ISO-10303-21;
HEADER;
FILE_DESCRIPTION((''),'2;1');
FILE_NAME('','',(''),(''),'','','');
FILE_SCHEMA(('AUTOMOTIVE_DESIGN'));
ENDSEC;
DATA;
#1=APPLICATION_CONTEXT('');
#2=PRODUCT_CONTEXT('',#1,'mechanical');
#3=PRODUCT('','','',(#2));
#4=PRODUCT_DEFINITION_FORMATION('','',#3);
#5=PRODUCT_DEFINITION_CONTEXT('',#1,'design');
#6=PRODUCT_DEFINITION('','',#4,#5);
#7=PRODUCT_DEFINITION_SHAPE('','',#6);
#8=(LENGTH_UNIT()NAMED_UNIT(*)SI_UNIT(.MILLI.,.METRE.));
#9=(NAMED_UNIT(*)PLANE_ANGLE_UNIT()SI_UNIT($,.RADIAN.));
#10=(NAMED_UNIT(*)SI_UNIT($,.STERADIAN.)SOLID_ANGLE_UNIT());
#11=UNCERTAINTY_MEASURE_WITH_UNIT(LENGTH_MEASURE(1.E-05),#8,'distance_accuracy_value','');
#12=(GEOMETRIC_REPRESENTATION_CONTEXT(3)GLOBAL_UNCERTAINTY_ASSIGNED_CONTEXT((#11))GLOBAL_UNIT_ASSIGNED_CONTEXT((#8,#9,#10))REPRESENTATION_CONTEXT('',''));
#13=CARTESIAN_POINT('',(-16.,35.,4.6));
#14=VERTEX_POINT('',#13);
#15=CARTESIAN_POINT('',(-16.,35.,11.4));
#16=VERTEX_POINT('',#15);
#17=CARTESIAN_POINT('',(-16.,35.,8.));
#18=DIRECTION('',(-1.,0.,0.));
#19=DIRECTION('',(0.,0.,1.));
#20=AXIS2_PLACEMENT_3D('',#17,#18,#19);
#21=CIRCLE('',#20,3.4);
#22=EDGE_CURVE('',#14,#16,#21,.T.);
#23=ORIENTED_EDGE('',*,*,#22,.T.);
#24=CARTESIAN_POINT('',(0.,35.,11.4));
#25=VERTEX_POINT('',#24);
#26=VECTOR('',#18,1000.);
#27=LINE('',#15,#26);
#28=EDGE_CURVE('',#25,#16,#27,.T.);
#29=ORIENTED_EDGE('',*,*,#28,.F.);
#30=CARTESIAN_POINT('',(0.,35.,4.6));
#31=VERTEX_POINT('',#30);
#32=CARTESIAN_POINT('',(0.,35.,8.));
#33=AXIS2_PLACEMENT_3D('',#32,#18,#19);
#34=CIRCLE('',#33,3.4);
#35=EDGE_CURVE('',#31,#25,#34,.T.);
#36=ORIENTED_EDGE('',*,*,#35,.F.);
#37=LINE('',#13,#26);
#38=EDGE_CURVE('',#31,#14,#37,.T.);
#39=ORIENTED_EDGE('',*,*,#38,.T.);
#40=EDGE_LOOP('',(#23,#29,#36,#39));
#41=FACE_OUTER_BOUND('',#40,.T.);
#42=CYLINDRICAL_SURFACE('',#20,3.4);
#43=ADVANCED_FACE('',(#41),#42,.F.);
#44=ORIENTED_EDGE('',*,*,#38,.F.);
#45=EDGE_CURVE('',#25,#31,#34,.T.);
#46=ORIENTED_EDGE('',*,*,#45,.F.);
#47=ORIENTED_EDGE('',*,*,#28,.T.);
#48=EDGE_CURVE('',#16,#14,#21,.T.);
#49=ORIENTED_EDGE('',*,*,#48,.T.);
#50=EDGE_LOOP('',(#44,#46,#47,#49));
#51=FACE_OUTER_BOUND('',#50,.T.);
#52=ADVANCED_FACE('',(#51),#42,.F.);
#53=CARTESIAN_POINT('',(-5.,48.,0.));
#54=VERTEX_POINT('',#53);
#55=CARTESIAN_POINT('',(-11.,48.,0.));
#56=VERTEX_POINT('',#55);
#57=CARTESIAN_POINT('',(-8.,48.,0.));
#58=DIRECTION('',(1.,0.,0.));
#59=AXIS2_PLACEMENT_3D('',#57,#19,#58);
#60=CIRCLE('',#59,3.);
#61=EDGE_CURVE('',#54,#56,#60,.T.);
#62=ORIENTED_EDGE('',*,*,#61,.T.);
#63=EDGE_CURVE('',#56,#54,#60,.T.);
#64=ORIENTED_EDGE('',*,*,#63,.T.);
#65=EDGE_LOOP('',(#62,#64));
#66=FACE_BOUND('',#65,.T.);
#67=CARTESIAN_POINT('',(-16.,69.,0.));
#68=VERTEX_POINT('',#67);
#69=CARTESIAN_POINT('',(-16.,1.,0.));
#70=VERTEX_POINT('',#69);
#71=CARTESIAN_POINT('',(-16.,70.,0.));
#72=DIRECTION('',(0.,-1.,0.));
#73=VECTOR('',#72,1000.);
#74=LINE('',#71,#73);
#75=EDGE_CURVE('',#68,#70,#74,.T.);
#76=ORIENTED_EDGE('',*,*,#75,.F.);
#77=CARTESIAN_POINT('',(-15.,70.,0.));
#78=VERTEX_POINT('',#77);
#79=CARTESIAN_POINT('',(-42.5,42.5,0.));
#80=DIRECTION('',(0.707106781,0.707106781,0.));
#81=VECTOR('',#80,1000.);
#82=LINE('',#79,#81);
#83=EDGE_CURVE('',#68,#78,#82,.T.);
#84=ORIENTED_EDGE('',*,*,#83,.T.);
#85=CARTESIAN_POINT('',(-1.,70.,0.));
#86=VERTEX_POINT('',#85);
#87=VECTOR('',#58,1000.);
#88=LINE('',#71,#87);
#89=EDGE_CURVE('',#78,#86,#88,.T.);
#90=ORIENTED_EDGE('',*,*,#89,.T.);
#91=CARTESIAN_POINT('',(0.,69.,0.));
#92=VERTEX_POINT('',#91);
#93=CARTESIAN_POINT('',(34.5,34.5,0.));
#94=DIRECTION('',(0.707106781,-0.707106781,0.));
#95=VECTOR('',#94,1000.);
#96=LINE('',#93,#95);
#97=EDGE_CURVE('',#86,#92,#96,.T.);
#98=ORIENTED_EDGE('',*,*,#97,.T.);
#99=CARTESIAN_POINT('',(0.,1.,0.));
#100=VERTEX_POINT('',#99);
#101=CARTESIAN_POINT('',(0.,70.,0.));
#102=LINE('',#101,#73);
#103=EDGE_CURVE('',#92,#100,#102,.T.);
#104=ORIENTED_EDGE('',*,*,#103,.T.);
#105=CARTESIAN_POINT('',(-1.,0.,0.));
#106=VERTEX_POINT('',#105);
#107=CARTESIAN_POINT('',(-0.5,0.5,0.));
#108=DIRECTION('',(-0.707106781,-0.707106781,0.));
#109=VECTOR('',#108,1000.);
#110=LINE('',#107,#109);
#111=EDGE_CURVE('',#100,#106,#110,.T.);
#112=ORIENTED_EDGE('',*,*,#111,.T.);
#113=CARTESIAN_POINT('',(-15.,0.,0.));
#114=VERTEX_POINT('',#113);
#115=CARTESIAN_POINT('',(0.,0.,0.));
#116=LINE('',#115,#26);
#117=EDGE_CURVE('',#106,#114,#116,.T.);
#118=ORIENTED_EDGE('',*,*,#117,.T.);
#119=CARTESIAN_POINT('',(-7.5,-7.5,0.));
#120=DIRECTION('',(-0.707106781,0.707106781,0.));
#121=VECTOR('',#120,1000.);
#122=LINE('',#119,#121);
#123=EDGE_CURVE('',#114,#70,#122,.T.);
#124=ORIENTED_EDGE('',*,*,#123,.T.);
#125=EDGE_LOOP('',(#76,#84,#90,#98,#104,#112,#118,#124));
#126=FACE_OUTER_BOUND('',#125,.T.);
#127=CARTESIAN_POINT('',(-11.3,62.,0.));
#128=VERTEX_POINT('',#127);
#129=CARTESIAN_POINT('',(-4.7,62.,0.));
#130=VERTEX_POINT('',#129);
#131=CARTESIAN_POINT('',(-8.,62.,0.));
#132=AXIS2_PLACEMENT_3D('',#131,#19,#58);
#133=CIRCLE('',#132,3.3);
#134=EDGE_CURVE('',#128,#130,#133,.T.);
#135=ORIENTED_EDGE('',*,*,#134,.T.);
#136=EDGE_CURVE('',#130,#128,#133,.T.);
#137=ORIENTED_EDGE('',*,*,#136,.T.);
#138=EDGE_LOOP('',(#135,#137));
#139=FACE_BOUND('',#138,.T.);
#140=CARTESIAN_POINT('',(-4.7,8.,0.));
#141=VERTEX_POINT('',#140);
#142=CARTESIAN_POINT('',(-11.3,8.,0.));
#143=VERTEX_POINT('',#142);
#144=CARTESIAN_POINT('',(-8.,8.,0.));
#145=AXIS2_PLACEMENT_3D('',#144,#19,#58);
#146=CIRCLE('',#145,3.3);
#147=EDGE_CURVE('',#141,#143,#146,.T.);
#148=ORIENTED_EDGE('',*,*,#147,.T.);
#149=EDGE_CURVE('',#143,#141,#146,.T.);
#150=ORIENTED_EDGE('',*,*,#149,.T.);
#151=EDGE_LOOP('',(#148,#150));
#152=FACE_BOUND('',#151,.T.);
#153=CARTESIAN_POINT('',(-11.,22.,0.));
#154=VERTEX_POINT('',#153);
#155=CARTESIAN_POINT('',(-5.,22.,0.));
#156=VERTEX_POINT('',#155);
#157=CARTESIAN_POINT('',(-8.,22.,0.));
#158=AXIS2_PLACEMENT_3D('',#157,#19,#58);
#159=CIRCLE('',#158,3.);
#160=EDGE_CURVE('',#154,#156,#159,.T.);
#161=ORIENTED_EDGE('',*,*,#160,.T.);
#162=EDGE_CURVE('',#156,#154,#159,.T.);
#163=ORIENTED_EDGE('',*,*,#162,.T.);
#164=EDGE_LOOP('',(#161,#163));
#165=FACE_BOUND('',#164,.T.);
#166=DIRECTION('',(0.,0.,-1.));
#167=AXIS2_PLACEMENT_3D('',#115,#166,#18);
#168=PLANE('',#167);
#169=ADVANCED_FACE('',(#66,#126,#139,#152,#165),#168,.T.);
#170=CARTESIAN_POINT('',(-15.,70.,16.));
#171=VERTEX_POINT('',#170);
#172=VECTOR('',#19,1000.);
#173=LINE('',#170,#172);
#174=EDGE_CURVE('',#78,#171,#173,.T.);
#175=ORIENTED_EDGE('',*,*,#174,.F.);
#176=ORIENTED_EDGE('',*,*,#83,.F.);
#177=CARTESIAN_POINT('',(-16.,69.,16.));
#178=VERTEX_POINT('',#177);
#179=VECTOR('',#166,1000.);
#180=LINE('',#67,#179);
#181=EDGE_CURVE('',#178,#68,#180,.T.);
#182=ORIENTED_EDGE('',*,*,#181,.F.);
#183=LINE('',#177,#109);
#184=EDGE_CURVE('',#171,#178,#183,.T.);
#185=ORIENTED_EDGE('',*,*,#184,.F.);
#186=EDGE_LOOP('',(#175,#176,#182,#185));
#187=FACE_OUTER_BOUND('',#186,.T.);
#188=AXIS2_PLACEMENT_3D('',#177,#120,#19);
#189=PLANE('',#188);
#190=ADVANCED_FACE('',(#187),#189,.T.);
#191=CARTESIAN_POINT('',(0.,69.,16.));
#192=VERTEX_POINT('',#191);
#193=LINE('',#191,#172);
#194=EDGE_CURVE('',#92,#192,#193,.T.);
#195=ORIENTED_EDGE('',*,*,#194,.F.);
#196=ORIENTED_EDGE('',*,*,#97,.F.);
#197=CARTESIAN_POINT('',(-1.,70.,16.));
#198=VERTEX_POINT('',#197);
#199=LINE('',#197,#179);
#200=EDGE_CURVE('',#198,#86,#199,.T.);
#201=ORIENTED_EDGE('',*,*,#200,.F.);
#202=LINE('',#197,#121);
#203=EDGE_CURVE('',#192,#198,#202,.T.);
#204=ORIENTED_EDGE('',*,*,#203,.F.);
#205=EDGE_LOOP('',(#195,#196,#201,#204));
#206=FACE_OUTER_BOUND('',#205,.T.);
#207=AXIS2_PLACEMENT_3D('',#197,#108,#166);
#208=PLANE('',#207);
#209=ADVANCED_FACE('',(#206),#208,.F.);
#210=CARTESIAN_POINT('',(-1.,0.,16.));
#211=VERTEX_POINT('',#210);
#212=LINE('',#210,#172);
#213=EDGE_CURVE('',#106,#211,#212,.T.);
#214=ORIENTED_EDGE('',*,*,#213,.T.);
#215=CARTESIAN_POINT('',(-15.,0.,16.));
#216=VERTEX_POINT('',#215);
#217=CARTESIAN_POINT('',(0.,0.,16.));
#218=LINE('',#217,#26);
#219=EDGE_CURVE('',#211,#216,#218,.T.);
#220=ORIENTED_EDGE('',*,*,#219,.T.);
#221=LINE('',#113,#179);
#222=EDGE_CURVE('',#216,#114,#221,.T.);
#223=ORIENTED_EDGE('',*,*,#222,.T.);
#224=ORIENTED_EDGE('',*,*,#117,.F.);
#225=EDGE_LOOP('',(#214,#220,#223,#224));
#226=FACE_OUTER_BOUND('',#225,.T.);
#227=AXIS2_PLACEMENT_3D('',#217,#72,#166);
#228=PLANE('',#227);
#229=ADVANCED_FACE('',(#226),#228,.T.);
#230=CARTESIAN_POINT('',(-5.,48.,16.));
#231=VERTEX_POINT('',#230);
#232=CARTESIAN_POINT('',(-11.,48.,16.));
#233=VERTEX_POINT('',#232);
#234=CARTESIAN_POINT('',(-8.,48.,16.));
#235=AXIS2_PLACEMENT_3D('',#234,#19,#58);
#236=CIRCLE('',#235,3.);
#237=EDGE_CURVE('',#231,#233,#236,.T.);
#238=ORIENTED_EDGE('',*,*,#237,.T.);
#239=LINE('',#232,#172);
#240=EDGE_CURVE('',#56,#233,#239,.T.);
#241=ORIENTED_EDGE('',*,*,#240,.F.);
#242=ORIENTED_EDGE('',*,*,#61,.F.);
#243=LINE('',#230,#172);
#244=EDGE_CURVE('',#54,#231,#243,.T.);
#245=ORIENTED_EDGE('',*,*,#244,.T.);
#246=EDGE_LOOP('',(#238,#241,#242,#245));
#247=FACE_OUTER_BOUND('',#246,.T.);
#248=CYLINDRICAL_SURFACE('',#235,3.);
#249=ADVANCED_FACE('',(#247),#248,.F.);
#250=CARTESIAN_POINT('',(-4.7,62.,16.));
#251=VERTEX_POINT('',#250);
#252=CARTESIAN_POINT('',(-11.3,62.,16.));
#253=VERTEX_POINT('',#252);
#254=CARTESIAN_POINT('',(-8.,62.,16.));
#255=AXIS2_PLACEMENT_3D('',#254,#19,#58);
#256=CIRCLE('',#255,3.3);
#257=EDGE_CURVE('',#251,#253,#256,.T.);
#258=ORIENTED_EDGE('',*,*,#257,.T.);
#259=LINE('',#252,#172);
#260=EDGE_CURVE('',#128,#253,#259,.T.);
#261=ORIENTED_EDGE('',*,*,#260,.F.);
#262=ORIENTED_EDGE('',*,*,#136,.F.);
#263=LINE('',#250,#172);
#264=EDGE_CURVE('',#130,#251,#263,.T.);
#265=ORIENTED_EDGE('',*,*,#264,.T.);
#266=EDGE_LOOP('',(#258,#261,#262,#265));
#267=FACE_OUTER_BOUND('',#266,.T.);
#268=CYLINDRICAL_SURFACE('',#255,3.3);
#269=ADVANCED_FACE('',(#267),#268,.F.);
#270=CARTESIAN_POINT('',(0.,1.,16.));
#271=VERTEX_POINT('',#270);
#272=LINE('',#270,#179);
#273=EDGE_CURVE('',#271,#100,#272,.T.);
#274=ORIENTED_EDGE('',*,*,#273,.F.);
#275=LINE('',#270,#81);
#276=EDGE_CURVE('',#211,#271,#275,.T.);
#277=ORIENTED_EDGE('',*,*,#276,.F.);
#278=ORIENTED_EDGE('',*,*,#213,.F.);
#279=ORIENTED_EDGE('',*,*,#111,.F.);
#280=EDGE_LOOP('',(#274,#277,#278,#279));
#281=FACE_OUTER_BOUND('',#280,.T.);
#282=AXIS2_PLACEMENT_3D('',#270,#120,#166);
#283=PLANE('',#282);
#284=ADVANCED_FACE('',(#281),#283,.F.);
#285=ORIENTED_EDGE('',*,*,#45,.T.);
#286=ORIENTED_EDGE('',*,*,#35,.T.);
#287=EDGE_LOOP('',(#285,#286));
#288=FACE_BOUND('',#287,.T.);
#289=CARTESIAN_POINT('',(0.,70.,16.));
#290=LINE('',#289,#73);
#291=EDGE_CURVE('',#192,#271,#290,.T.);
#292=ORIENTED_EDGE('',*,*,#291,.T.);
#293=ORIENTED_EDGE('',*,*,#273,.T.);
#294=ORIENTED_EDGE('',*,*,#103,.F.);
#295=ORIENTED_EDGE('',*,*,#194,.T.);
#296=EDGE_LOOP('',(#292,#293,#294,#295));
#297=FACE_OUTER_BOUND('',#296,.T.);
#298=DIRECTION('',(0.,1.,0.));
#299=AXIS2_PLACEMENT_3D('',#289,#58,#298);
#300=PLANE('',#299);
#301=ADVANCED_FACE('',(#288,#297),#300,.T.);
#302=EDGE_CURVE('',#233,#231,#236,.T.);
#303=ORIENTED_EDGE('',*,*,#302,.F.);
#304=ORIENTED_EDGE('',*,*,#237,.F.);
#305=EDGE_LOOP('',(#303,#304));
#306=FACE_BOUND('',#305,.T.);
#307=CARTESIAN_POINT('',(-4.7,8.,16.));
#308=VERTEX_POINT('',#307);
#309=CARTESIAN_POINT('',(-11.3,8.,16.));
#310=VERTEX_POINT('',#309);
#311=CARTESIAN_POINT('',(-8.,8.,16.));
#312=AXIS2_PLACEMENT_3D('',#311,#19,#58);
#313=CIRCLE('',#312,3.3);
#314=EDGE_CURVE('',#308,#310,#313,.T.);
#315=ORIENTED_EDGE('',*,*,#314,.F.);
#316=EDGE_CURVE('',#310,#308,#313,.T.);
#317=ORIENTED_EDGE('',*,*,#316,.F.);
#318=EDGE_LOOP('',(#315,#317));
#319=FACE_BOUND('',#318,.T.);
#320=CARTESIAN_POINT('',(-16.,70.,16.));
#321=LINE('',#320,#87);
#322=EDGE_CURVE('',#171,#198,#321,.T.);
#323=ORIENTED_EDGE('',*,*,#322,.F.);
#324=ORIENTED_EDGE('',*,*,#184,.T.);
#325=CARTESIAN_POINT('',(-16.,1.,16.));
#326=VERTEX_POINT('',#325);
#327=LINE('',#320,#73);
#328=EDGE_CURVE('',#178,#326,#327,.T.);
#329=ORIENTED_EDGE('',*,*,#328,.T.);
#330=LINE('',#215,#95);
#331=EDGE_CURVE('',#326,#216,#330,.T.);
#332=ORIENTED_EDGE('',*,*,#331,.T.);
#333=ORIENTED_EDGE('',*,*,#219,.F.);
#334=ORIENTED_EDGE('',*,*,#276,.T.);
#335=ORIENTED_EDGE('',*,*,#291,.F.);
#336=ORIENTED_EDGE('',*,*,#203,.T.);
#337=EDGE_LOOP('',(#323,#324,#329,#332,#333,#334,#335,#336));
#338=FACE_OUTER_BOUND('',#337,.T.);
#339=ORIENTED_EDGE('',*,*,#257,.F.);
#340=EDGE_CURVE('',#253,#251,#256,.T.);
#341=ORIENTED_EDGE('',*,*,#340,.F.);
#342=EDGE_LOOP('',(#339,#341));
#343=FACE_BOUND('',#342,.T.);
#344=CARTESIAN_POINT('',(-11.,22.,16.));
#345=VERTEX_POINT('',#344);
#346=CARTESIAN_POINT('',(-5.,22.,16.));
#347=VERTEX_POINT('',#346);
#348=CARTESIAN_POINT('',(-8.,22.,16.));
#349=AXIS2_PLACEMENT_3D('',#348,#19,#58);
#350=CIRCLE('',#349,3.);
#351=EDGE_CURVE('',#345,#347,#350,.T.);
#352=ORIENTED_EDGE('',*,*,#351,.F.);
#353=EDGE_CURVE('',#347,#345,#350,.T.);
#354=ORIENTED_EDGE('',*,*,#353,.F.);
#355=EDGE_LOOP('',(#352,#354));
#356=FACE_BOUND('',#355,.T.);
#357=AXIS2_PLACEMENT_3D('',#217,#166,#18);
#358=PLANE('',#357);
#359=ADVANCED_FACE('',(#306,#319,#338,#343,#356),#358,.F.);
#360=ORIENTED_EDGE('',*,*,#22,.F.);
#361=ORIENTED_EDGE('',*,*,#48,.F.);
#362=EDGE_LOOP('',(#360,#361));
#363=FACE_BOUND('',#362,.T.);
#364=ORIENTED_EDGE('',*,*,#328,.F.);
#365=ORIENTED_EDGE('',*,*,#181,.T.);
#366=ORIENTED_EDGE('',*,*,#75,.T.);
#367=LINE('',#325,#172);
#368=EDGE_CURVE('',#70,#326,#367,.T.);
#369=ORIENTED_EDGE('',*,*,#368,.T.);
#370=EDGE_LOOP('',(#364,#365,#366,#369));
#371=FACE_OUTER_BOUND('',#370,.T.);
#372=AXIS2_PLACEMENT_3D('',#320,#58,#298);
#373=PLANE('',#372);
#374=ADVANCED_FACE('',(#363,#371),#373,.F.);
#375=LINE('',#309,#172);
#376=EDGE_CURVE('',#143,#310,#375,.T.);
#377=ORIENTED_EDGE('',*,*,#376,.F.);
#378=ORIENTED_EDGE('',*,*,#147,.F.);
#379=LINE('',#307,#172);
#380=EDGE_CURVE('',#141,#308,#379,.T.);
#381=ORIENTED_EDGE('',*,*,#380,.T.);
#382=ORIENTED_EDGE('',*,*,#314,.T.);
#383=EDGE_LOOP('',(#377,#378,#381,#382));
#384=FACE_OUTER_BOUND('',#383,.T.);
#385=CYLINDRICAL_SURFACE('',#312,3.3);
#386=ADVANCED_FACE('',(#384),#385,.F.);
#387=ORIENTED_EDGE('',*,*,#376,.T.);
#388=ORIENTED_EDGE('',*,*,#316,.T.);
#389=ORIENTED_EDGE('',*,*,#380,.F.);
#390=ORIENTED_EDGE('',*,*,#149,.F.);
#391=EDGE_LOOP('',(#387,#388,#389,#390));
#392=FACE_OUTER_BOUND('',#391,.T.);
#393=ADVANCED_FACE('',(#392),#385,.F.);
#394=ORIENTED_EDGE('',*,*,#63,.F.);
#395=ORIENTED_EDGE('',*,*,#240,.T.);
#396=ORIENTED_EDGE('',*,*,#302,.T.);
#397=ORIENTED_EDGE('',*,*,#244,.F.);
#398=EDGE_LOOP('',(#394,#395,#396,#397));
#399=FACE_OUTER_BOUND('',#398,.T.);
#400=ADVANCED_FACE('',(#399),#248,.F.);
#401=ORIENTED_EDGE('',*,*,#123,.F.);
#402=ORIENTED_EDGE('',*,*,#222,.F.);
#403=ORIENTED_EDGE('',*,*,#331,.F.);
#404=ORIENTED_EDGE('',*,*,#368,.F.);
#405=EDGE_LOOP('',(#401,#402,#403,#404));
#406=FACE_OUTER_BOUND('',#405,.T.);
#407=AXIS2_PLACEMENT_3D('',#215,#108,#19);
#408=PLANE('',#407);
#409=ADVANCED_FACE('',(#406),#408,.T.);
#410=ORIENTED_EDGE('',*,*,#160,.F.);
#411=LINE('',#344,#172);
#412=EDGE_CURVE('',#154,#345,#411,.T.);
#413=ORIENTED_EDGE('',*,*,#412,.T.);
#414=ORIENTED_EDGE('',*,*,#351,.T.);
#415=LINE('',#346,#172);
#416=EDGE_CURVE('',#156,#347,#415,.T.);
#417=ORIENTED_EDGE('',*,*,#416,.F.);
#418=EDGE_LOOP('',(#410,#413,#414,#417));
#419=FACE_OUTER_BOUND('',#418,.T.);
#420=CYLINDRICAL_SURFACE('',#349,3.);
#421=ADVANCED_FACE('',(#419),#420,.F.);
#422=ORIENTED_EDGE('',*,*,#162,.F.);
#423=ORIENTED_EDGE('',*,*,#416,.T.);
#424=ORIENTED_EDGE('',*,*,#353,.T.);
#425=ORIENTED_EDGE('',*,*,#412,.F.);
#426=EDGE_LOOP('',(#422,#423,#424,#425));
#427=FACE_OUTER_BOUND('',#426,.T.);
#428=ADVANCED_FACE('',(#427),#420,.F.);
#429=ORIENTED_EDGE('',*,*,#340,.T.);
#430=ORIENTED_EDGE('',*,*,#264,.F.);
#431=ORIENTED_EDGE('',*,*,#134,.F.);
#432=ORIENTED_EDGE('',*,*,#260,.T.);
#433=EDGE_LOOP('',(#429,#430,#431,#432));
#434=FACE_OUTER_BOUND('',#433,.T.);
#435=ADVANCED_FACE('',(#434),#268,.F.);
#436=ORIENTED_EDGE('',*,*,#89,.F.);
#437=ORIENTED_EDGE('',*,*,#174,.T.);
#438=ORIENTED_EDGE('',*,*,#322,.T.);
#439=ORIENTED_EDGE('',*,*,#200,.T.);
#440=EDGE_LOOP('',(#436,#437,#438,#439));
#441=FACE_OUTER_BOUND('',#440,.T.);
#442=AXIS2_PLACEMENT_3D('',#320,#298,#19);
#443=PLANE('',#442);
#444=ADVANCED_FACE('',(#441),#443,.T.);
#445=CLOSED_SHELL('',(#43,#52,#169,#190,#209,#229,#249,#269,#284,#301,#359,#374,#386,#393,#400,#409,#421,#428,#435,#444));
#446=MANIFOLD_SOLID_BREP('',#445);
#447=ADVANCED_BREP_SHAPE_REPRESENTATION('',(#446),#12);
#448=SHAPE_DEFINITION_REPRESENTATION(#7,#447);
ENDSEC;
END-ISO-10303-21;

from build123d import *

# Parameters (mm, degrees)
SKETCH1_W                    = 16
SKETCH1_H                    = 70
EXTRUDE_THIN1_DEPTH          = 16
CHAMFER1_SIZE                = 1
SIZE_MM_BLIND_DOWEL_HOLE_1_D = 6
M8_TAPPED_HOLE1_D            = 6.8
M6_CLEARANCE_HOLE1_D         = 6.6


with BuildPart() as part:
    # Sketch1 → Extrude-Thin1 (new body)
    with BuildSketch(Plane.XY):
        with Locations((-8, 35)):
            Rectangle(SKETCH1_W, SKETCH1_H)
    extrude(amount=EXTRUDE_THIN1_DEPTH)

    # Chamfer1
    chamfer1_edges = [part.edges().sort_by_distance(p)[0] for p in [
        (-16, 70, 8),
        (0, 70, 8),
        (0, 0, 8),
        (-16, 0, 8),
    ]]
    chamfer(chamfer1_edges, length=CHAMFER1_SIZE)

    # Size mm blind dowel hole 1 (through all)
    with Locations(Plane.XY.offset(16)):
        with Locations((-8, 48), (-8, 22)):
            Hole(SIZE_MM_BLIND_DOWEL_HOLE_1_D / 2)

    # M8 Tapped Hole1 (through all)
    with Locations(Plane.ZY.offset(16)):
        with Locations((8, 35)):
            Hole(M8_TAPPED_HOLE1_D / 2)

    # M6 Clearance Hole1 (through all)
    with Locations(Plane.XY.offset(16)):
        with Locations((-8, 62), (-8, 8)):
            Hole(M6_CLEARANCE_HOLE1_D / 2)


solid = part.part
